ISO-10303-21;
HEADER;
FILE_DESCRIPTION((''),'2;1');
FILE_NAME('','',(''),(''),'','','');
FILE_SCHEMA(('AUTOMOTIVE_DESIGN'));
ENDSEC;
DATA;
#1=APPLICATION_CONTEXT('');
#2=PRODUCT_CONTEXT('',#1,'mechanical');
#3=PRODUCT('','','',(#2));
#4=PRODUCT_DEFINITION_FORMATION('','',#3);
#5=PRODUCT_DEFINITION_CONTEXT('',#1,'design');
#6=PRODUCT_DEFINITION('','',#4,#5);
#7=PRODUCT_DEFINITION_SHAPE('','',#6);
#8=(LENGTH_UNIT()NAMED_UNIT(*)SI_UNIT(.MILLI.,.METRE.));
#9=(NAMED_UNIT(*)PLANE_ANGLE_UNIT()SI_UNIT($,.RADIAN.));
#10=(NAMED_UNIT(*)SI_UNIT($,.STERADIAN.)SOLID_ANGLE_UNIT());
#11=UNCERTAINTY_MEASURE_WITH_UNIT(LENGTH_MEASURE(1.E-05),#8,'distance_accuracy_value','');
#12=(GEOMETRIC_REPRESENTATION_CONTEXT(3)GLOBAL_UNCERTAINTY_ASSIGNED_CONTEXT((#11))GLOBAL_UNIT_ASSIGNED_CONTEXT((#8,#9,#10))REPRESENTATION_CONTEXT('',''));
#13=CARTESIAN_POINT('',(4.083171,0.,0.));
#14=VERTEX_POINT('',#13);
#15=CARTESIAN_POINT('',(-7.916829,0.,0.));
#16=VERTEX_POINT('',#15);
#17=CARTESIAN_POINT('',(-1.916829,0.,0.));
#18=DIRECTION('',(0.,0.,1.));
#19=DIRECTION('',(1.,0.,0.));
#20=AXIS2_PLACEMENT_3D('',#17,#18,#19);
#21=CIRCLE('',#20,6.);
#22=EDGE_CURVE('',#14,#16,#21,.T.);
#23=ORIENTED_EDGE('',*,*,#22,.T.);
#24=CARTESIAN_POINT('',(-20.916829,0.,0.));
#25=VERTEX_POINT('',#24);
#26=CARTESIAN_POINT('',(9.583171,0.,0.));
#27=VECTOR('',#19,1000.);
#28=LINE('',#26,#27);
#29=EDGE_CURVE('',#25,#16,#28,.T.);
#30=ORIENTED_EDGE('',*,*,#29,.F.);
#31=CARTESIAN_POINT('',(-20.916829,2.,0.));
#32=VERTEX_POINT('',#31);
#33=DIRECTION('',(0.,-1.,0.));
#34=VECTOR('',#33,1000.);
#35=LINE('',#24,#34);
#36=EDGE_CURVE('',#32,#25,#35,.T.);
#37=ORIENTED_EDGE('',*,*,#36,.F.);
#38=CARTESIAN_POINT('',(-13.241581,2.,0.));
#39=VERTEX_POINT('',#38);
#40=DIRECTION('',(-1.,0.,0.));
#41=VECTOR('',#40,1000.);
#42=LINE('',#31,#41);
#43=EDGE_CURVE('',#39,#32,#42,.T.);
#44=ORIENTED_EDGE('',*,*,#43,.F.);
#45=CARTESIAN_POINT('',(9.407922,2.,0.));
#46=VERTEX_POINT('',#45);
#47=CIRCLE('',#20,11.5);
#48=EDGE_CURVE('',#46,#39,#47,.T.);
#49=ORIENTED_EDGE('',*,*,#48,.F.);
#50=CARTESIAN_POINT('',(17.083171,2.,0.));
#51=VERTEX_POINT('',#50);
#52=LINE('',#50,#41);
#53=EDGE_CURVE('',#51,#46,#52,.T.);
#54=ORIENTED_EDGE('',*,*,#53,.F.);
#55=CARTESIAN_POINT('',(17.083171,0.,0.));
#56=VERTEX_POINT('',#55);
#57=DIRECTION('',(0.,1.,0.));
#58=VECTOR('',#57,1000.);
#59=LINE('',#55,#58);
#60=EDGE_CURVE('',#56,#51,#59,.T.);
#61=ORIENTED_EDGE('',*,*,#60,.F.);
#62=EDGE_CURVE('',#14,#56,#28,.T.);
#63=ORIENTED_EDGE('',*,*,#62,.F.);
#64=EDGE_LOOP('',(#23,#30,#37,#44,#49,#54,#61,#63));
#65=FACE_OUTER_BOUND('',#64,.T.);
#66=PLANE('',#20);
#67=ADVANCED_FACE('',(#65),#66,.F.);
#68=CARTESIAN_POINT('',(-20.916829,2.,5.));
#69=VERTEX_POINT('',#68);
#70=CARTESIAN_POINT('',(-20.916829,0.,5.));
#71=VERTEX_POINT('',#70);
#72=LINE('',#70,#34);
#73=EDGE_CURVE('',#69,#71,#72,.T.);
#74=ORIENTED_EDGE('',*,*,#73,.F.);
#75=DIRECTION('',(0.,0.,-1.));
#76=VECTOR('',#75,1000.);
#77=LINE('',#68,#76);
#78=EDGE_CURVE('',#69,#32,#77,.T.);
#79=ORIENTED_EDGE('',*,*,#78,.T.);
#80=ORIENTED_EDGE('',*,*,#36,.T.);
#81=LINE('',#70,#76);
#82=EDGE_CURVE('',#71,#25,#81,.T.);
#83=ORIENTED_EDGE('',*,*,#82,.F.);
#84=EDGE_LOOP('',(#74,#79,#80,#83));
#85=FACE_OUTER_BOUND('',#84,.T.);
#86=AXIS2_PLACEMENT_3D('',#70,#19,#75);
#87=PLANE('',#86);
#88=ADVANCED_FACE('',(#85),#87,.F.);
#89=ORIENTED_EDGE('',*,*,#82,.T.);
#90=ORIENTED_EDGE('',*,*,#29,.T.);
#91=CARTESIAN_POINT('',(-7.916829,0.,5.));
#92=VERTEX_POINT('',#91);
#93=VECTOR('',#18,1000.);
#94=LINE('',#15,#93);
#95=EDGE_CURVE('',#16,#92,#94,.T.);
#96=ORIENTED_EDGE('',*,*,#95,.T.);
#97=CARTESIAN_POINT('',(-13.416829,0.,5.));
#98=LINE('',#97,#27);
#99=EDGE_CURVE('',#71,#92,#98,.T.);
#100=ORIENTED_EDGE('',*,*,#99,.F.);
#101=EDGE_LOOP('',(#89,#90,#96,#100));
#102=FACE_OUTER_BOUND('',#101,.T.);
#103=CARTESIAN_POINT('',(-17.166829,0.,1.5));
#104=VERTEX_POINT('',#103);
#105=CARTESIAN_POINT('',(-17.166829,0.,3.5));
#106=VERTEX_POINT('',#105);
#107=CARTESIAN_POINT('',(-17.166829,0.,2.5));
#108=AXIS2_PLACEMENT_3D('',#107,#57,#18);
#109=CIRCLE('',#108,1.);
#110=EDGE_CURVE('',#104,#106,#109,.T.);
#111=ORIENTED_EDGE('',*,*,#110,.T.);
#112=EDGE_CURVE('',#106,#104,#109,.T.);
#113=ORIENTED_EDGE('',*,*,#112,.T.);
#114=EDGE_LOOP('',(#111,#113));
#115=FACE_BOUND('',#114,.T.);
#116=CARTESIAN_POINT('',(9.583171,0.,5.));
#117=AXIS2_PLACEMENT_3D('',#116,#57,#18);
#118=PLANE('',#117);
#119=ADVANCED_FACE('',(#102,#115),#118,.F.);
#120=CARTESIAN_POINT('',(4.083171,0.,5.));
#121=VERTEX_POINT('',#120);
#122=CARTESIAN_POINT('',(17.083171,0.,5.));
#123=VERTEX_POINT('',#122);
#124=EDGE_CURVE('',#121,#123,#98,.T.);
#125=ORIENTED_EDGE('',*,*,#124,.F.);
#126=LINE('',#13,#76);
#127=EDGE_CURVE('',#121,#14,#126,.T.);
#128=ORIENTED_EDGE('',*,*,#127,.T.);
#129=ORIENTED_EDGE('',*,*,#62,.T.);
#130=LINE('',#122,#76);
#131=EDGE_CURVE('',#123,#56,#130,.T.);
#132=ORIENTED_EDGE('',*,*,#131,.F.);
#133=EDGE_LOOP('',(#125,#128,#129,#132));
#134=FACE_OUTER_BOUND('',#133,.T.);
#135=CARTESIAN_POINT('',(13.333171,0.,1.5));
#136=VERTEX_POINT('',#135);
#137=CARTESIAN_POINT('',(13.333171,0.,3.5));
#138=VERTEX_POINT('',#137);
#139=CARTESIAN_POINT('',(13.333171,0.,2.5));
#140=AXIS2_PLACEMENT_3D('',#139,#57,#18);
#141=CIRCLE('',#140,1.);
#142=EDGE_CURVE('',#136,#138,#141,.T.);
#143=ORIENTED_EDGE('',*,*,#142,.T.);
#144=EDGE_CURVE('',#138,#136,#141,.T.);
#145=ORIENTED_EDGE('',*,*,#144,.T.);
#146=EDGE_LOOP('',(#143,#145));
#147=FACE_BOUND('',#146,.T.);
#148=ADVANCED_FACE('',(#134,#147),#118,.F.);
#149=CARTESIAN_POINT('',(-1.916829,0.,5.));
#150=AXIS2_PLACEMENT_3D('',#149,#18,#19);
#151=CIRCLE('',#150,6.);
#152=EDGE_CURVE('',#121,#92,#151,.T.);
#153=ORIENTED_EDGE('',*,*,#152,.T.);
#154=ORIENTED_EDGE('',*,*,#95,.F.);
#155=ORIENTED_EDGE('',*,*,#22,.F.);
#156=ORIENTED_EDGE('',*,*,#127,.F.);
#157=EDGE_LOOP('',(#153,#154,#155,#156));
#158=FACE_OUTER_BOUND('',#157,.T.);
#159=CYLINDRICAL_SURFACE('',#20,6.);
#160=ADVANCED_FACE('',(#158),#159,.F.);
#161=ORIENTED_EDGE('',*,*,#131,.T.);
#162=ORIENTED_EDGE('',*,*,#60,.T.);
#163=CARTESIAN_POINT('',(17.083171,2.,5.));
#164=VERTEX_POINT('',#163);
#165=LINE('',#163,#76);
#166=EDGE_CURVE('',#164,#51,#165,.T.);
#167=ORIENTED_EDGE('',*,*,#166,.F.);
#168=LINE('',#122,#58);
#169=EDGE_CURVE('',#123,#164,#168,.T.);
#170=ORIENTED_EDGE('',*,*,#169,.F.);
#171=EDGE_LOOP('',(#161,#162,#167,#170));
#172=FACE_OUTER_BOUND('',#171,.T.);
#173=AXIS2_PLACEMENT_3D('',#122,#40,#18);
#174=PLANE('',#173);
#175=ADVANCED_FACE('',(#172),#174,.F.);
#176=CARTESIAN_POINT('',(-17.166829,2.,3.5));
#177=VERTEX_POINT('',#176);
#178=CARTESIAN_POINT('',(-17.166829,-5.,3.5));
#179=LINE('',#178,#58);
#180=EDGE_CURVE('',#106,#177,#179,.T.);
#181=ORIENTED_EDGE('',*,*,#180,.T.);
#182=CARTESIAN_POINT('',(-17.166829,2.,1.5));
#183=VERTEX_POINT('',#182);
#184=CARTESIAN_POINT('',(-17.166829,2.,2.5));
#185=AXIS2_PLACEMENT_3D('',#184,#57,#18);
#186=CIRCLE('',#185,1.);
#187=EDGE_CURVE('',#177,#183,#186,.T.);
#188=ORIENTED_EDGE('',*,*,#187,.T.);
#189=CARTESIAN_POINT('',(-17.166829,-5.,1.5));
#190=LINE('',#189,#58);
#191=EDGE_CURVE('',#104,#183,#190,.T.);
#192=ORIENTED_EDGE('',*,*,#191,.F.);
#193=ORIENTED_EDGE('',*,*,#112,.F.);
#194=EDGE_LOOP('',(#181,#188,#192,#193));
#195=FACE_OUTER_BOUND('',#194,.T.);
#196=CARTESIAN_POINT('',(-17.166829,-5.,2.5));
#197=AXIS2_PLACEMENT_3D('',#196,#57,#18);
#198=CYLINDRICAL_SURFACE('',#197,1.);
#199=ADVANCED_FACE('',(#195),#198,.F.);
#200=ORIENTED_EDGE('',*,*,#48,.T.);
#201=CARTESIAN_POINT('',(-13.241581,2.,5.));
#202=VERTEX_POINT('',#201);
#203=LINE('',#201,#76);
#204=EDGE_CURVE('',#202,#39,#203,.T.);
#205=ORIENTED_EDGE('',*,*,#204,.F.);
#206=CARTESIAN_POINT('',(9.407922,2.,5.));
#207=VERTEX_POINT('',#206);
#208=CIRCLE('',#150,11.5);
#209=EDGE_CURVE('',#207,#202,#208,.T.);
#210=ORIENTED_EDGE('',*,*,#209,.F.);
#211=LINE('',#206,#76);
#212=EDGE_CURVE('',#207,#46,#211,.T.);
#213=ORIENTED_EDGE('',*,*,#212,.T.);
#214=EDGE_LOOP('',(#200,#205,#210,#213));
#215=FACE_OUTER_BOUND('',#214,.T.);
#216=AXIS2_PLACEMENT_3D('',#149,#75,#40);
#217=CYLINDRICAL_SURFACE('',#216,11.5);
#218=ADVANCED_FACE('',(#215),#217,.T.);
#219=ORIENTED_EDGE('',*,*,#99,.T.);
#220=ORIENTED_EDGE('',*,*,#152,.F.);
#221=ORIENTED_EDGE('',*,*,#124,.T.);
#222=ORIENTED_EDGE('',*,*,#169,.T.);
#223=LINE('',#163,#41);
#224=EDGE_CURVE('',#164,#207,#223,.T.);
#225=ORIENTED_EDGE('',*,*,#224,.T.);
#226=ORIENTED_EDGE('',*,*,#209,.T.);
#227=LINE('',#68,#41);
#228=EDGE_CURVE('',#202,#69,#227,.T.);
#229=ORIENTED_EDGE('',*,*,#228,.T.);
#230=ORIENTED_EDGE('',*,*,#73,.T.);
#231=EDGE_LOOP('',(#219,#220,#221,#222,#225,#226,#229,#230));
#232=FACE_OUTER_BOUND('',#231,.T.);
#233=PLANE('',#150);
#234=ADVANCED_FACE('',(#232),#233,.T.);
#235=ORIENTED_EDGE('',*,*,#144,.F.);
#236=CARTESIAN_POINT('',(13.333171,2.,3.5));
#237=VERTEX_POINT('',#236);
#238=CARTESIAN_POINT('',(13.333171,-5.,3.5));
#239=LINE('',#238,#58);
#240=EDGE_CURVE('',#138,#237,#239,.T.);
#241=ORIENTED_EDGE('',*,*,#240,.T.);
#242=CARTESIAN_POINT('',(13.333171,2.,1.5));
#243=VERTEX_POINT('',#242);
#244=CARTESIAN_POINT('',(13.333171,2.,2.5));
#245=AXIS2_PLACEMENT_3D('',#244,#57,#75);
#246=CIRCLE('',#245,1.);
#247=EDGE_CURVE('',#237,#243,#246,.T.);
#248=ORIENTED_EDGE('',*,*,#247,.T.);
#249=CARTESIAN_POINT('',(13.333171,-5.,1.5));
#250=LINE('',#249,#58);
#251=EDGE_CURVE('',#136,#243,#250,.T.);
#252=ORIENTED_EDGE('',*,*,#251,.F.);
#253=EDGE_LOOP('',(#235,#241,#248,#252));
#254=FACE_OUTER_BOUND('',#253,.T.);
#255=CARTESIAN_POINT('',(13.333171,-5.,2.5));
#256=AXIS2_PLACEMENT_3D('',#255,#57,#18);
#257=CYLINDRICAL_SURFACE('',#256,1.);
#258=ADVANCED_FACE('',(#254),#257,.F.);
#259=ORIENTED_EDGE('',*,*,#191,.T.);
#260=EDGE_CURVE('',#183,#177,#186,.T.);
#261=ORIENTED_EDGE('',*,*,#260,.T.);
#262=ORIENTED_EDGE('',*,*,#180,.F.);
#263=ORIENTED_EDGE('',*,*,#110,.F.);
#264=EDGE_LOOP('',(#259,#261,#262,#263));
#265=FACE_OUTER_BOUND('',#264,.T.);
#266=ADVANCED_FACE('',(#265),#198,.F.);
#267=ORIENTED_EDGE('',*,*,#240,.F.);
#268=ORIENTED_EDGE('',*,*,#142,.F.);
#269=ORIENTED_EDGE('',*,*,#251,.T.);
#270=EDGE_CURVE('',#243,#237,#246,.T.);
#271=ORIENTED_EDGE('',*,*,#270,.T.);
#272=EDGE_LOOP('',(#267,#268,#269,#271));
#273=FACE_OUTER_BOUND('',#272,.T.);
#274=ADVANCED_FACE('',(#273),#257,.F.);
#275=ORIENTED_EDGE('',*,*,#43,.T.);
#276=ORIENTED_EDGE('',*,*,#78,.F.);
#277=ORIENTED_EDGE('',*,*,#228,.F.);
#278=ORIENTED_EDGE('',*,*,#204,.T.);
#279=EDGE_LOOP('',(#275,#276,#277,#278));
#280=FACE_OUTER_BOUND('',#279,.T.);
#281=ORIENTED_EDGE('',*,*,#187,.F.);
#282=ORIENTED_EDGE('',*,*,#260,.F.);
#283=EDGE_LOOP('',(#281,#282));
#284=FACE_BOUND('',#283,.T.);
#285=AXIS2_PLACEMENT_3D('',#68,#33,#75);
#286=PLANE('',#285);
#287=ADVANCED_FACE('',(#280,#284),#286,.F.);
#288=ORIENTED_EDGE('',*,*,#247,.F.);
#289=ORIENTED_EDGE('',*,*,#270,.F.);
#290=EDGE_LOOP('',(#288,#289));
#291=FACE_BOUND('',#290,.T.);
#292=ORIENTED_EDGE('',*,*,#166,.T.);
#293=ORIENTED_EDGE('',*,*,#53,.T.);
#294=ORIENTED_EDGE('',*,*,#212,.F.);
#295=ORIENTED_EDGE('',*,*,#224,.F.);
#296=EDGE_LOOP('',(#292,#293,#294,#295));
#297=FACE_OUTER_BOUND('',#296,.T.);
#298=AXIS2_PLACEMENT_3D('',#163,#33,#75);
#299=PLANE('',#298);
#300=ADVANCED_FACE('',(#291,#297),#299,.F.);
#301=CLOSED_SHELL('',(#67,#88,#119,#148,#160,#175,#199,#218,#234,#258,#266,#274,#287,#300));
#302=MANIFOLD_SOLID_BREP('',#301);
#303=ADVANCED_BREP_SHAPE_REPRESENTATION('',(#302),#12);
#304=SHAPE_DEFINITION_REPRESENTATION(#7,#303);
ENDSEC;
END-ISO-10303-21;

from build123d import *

# Parameters (mm, degrees)
BOSS_EXTRUDE1_DEPTH = 5
SKETCH3_R           = 1
CUT_EXTRUDE2_DEPTH  = 7
SKETCH4_R           = 6
CUT_EXTRUDE3_DEPTH  = 25.38777855


with BuildPart() as part:
    # Sketch2 → Boss-Extrude1 (new body)
    with BuildSketch(Plane.XY):
        with BuildLine():
            Line((9.583170828, 0), (17.083170828, 0))
            Line((17.083170828, 0), (17.083170828, 2))
            Line((17.083170828, 2), (9.407922481, 2))
            ThreePointArc((9.407922481, 2), (-1.916829172, 11.5), (-13.241580825, 2))
            Line((-13.241580825, 2), (-20.916829172, 2))
            Line((-20.916829172, 2), (-20.916829172, 0))
            Line((-20.916829172, 0), (-13.416829172, 0))
            Line((-13.416829172, 0), (-7.916829172, 0))
            Line((-7.916829172, 0), (4.083170828, 0))
            Line((4.083170828, 0), (9.583170828, 0))
        make_face()
    extrude(amount=BOSS_EXTRUDE1_DEPTH)

    # Sketch3 → Cut-Extrude2 (cut)
    with BuildSketch(Plane(origin=(0, 2, 0), x_dir=(1, 0, 0), z_dir=(0, 1, 0))):
        with Locations(Location((-17.166829172, -2.5, 0), (0, 0, 270))):
            Circle(SKETCH3_R)
        with Locations(Location((13.333170828, -2.5, 0), (0, 0, 270))):
            Circle(SKETCH3_R)
    extrude(amount=-CUT_EXTRUDE2_DEPTH, mode=Mode.SUBTRACT)

    # Sketch4 → Cut-Extrude3 (cut, through all)
    with BuildSketch(Plane.XY.offset(5)):
        with Locations((-1.916829172, 0)):
            Circle(SKETCH4_R)
    extrude(amount=-CUT_EXTRUDE3_DEPTH, mode=Mode.SUBTRACT)


solid = part.part
